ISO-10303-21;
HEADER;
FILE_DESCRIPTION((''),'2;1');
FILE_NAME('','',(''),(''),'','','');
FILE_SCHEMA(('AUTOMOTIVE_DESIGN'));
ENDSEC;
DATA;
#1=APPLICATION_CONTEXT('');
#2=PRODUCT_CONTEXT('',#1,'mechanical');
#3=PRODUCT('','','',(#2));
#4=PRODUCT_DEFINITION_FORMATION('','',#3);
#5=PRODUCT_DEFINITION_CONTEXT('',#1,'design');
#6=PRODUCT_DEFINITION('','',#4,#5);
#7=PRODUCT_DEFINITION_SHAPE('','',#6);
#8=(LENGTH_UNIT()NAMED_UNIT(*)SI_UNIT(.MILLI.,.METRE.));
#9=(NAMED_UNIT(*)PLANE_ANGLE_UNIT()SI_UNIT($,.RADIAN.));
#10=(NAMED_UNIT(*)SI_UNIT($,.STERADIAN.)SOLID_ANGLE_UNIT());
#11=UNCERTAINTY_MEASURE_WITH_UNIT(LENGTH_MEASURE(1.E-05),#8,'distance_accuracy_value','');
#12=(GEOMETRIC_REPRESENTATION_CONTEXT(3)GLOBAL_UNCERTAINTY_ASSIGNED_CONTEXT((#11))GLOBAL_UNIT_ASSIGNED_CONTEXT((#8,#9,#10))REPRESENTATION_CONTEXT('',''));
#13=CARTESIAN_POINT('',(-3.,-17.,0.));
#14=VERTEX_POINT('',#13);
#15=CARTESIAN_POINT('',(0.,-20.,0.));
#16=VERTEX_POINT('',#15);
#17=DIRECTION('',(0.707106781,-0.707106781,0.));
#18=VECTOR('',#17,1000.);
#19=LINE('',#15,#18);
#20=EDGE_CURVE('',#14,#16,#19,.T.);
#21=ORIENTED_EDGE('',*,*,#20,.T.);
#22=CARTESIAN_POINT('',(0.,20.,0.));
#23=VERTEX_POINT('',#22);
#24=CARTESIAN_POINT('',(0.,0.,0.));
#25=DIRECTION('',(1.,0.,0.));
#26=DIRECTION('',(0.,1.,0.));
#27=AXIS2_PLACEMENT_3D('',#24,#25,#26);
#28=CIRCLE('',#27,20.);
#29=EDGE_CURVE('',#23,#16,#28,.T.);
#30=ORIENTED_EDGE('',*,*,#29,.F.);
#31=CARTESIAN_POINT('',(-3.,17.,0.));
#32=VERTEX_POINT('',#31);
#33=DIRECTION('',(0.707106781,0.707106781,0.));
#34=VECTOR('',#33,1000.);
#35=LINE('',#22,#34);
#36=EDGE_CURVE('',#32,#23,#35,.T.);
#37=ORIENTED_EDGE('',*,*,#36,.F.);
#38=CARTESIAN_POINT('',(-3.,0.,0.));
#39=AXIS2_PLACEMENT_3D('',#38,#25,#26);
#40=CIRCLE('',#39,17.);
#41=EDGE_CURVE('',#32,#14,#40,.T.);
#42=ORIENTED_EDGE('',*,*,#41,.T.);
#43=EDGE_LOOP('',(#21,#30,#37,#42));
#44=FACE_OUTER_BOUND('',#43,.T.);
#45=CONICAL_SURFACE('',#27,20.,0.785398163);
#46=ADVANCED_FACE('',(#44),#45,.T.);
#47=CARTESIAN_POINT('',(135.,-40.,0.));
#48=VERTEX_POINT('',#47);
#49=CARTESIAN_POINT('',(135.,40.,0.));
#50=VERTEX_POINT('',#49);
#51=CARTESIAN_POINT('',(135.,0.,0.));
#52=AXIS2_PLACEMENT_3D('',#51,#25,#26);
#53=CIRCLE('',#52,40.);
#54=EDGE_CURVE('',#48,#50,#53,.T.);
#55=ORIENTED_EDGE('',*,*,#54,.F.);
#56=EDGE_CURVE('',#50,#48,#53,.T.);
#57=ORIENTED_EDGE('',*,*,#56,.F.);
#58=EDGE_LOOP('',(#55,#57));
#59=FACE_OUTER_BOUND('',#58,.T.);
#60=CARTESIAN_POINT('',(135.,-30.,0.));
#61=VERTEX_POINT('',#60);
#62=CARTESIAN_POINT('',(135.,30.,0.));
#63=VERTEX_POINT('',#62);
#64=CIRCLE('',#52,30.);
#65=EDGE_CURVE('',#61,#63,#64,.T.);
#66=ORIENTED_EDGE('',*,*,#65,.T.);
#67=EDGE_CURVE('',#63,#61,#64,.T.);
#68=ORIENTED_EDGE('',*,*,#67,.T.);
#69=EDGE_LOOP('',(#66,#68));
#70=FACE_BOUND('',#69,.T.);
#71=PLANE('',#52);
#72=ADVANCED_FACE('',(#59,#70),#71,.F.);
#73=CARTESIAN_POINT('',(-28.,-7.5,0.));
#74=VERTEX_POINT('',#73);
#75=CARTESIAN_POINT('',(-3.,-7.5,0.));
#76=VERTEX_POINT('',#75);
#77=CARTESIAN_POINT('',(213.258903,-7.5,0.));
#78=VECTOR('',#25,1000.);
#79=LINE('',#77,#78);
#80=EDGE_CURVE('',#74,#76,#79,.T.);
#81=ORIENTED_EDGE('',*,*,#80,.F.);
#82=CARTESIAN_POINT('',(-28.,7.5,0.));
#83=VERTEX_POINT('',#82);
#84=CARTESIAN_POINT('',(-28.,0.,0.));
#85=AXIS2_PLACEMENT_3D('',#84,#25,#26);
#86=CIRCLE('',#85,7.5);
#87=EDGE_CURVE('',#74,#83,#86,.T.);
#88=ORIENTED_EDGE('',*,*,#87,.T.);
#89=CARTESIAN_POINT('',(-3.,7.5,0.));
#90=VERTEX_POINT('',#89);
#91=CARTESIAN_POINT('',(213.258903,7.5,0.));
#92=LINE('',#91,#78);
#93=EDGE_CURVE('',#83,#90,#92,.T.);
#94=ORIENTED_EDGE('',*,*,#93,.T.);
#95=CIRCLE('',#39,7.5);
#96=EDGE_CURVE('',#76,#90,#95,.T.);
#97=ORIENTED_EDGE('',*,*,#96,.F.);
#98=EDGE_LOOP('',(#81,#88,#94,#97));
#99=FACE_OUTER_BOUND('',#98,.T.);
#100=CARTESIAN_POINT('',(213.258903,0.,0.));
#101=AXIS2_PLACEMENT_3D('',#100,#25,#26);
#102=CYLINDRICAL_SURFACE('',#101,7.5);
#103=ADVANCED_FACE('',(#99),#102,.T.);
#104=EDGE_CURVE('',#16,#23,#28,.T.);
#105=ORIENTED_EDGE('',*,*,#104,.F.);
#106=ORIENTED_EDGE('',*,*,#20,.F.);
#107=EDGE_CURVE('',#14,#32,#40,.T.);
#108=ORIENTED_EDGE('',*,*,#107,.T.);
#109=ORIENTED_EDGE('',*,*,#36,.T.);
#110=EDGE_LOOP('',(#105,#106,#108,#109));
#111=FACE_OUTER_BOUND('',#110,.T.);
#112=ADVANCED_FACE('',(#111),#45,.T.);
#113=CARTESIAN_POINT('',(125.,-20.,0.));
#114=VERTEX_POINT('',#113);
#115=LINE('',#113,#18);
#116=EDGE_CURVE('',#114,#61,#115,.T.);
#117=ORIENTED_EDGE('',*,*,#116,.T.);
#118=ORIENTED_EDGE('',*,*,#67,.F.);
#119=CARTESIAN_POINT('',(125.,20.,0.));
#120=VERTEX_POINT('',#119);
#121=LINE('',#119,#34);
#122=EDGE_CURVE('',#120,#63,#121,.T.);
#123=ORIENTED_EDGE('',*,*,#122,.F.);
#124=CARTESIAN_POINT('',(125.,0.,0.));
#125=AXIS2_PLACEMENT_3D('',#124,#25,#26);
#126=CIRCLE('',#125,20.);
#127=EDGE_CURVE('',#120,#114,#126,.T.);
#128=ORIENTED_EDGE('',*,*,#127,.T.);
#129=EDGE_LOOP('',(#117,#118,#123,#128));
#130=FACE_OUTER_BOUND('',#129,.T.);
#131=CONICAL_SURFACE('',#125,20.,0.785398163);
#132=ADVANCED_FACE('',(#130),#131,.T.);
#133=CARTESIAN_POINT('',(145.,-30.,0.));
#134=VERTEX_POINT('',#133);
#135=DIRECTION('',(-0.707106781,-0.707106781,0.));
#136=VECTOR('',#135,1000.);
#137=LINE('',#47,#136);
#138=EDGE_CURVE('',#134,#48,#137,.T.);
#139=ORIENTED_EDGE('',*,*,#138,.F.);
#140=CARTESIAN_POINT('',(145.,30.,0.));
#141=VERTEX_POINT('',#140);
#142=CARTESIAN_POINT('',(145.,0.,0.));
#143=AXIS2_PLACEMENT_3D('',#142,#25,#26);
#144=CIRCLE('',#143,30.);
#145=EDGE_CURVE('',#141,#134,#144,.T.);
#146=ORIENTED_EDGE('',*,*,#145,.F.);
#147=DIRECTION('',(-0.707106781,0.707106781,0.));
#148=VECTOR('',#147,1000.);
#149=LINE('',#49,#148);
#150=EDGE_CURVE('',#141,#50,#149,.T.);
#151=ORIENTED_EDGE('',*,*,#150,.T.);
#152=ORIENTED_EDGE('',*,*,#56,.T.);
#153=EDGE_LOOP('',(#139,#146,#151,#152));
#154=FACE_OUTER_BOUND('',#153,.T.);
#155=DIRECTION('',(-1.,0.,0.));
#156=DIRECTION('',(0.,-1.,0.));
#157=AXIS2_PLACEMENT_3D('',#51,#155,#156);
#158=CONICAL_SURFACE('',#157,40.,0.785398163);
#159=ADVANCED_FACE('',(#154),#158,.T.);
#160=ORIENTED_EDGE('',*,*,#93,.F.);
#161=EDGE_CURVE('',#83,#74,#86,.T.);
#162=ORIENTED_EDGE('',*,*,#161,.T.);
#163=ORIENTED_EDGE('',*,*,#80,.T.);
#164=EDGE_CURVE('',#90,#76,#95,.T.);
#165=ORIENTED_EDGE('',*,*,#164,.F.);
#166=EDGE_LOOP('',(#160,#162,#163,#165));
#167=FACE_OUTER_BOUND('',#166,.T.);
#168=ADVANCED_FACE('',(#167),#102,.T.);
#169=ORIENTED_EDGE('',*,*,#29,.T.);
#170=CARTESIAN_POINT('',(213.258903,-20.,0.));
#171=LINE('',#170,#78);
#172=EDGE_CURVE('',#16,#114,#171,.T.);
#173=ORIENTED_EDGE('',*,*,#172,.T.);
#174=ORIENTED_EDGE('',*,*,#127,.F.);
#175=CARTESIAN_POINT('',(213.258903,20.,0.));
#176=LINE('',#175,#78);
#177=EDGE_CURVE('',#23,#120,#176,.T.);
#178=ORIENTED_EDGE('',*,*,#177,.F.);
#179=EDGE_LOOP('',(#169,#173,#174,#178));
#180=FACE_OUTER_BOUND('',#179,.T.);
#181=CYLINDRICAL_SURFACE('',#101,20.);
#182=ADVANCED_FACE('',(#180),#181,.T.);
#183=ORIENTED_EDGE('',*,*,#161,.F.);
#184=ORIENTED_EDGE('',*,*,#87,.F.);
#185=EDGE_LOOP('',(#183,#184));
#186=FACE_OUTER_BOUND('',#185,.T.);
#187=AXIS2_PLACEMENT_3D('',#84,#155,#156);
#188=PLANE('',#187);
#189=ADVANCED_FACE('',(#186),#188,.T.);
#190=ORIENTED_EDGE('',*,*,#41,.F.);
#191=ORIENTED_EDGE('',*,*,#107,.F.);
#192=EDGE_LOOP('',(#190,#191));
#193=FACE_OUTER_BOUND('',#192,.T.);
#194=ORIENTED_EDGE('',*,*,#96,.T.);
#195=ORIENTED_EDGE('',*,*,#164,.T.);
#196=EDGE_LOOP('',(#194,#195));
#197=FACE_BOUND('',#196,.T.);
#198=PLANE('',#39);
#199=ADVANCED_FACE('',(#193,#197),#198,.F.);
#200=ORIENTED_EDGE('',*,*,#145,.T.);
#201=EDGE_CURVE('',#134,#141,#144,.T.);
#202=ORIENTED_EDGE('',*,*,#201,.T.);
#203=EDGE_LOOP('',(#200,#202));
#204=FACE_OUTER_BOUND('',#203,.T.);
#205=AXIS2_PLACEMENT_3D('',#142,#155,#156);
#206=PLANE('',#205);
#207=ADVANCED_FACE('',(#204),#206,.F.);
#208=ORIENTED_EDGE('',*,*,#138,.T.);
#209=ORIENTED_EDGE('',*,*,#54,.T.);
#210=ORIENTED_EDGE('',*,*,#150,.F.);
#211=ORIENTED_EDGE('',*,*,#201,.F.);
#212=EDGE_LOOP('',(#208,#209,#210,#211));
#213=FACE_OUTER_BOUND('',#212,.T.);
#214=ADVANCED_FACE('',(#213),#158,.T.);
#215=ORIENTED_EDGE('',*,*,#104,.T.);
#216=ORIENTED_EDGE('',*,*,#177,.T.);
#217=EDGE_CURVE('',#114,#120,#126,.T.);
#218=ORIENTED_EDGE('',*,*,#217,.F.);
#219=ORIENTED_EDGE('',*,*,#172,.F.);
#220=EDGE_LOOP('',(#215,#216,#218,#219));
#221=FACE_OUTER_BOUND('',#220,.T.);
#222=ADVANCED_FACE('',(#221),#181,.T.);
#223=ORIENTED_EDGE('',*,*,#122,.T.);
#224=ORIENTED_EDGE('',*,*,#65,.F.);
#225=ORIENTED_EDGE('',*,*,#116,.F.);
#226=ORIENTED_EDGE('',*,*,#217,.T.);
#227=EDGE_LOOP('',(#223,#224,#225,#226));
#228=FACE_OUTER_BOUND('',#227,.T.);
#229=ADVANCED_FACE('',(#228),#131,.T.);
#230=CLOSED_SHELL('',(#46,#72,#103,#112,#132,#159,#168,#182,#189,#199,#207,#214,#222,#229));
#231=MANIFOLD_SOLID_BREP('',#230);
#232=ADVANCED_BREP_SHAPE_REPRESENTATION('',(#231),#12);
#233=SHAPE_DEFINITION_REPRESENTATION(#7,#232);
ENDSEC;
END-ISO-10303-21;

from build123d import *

# Parameters (mm, degrees)
PIN_PROFILE_SKETCH_W   = 25
PIN_PROFILE_SKETCH_H   = 7.5
PIN_PROFILE_SKETCH_W_2 = 125
PIN_PROFILE_SKETCH_H_2 = 20


with BuildPart() as part:
    # Pin Profile Sketch → Pin Body Revolve (revolve)
    with BuildSketch(Plane.XY):
        with Locations((-15.5, 3.75)):
            Rectangle(PIN_PROFILE_SKETCH_W, PIN_PROFILE_SKETCH_H)
        with Locations((62.5, 10)):
            Rectangle(PIN_PROFILE_SKETCH_W_2, PIN_PROFILE_SKETCH_H_2)
        Polygon((-3, 0), (0, 0), (0, 20), (-3, 17), (-3, 7.5), align=None)
        Polygon((125, 0), (135, 0), (135, 30), (125, 20), align=None)
        Polygon((135, 0), (145, 0), (145, 30), (135, 40), (135, 30), align=None)
    revolve(axis=Axis((213.258902513, 0, 0), (-1, 0, 0)))


solid = part.part
